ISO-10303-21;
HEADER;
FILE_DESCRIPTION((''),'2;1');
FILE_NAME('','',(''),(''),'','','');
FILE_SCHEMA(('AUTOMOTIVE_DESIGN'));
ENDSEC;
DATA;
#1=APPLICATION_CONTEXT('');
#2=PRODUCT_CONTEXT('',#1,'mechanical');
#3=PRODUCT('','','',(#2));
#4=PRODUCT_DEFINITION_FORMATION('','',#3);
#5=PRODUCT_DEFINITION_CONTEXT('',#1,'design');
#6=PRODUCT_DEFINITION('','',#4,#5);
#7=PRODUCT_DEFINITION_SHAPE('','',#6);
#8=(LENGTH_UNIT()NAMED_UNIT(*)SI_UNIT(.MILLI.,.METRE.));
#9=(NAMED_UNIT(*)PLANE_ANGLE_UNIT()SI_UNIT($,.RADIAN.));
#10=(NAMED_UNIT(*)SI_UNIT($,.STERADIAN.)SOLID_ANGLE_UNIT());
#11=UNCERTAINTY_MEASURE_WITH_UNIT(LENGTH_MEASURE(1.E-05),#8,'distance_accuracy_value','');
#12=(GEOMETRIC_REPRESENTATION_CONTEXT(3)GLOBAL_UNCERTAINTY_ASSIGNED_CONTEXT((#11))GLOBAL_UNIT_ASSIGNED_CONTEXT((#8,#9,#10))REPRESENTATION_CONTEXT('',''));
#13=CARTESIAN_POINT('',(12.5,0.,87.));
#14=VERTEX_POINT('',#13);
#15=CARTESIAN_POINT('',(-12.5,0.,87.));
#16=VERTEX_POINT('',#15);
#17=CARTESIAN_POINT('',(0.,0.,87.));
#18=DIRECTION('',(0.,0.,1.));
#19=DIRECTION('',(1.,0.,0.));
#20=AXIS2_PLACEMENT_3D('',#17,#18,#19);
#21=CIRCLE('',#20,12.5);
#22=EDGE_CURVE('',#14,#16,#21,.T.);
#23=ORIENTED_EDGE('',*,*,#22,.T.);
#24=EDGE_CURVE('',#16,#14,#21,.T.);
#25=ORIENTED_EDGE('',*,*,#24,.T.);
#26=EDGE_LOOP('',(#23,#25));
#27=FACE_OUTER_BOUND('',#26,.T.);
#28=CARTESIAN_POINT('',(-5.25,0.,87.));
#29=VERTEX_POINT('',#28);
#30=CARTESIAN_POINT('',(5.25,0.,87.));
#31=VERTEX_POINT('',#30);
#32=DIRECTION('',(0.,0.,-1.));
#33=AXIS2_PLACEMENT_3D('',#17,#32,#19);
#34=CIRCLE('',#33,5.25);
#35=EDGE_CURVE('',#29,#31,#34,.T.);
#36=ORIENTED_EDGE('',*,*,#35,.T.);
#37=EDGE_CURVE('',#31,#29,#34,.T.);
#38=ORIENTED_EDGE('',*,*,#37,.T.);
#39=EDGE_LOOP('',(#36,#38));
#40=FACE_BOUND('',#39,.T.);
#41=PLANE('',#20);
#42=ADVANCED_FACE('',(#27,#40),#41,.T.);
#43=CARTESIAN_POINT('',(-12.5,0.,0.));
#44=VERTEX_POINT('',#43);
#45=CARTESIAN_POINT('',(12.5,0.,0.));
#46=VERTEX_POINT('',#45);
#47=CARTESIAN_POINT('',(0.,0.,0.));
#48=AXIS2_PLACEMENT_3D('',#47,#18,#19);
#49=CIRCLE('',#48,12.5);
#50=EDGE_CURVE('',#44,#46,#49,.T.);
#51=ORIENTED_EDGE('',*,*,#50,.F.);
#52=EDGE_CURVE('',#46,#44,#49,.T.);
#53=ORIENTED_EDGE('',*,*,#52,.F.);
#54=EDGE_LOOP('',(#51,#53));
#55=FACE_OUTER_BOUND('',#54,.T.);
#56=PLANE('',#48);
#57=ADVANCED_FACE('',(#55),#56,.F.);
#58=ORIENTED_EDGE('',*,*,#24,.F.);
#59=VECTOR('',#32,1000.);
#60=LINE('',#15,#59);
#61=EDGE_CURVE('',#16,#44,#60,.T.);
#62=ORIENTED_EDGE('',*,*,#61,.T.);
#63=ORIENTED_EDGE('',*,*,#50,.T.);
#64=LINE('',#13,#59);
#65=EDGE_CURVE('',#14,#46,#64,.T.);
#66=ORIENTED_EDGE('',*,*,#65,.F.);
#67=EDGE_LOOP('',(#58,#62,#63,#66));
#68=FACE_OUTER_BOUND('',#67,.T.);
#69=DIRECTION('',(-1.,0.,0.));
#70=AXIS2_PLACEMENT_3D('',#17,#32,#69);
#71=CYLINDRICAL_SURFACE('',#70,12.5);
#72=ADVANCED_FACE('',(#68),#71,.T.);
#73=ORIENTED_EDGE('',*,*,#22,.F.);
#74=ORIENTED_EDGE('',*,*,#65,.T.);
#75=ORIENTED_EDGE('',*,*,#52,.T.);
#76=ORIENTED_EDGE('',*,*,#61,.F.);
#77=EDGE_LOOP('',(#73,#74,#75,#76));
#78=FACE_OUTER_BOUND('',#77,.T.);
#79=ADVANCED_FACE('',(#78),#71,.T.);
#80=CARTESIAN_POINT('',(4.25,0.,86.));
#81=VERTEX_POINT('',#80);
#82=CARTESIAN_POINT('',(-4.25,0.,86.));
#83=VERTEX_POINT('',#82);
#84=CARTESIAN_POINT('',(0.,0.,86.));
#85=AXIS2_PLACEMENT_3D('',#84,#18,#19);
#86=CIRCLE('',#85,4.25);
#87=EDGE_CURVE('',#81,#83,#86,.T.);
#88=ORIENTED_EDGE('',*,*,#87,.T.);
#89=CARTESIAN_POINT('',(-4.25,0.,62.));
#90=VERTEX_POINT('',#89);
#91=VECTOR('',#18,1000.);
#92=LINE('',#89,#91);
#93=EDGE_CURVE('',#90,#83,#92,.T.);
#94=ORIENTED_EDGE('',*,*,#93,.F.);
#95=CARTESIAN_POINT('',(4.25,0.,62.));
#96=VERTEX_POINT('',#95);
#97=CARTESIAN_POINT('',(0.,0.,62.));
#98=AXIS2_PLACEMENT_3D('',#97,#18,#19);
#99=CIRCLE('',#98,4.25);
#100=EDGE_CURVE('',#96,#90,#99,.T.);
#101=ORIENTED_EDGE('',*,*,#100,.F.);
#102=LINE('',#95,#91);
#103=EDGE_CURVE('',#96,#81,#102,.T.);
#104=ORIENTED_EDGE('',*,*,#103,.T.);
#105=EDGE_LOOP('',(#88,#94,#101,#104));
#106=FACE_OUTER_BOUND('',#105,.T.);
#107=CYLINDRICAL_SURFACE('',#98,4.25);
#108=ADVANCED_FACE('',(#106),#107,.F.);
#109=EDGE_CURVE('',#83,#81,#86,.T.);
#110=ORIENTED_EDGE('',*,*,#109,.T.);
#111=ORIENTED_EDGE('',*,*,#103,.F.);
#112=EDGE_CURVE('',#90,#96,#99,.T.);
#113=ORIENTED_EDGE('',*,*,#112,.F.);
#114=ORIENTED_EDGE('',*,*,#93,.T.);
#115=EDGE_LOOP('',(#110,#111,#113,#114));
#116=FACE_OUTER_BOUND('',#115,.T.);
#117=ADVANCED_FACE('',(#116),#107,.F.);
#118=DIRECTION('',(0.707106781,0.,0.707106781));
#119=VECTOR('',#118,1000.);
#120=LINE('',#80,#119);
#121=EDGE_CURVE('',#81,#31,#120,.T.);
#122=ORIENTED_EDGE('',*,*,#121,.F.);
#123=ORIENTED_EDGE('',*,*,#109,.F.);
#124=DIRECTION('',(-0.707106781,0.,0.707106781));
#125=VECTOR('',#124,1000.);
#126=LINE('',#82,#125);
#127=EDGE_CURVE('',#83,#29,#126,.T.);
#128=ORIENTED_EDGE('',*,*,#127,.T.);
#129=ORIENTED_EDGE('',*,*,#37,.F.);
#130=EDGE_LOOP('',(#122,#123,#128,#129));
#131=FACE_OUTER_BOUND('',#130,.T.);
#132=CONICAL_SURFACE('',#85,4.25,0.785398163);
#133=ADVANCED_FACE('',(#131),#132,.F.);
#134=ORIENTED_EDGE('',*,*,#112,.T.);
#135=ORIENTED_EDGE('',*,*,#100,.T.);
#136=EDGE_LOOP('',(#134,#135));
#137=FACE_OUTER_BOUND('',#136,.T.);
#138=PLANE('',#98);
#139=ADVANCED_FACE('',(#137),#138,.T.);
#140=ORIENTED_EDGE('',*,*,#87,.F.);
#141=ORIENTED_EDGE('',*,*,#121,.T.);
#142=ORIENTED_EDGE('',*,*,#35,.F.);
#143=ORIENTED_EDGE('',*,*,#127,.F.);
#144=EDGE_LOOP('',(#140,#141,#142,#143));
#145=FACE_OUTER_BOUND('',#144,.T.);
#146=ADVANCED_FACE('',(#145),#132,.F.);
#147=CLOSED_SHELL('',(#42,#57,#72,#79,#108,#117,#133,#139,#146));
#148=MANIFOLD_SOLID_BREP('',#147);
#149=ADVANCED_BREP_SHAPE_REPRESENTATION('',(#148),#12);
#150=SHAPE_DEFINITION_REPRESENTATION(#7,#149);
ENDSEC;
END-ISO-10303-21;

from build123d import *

# Parameters (mm, degrees)
SKETCH1_R           = 12.5
BOSS_EXTRUDE1_DEPTH = 87
SKETCH2_R           = 4.25
CUT_EXTRUDE1_DEPTH  = 25
CHAMFER1_SIZE       = 1


with BuildPart() as part:
    # Sketch1 → Boss-Extrude1 (new body)
    with BuildSketch(Plane.XY):
        Circle(SKETCH1_R)
    extrude(amount=BOSS_EXTRUDE1_DEPTH)

    # Sketch2 → Cut-Extrude1 (cut)
    with BuildSketch(Plane.XY.offset(87)):
        Circle(SKETCH2_R)
    extrude(amount=-CUT_EXTRUDE1_DEPTH, mode=Mode.SUBTRACT)

    # Chamfer1
    chamfer1_edges = [part.edges().sort_by_distance(p)[0] for p in [
        (-4.25, 0, 87),
    ]]
    chamfer(chamfer1_edges, length=CHAMFER1_SIZE)


solid = part.part
